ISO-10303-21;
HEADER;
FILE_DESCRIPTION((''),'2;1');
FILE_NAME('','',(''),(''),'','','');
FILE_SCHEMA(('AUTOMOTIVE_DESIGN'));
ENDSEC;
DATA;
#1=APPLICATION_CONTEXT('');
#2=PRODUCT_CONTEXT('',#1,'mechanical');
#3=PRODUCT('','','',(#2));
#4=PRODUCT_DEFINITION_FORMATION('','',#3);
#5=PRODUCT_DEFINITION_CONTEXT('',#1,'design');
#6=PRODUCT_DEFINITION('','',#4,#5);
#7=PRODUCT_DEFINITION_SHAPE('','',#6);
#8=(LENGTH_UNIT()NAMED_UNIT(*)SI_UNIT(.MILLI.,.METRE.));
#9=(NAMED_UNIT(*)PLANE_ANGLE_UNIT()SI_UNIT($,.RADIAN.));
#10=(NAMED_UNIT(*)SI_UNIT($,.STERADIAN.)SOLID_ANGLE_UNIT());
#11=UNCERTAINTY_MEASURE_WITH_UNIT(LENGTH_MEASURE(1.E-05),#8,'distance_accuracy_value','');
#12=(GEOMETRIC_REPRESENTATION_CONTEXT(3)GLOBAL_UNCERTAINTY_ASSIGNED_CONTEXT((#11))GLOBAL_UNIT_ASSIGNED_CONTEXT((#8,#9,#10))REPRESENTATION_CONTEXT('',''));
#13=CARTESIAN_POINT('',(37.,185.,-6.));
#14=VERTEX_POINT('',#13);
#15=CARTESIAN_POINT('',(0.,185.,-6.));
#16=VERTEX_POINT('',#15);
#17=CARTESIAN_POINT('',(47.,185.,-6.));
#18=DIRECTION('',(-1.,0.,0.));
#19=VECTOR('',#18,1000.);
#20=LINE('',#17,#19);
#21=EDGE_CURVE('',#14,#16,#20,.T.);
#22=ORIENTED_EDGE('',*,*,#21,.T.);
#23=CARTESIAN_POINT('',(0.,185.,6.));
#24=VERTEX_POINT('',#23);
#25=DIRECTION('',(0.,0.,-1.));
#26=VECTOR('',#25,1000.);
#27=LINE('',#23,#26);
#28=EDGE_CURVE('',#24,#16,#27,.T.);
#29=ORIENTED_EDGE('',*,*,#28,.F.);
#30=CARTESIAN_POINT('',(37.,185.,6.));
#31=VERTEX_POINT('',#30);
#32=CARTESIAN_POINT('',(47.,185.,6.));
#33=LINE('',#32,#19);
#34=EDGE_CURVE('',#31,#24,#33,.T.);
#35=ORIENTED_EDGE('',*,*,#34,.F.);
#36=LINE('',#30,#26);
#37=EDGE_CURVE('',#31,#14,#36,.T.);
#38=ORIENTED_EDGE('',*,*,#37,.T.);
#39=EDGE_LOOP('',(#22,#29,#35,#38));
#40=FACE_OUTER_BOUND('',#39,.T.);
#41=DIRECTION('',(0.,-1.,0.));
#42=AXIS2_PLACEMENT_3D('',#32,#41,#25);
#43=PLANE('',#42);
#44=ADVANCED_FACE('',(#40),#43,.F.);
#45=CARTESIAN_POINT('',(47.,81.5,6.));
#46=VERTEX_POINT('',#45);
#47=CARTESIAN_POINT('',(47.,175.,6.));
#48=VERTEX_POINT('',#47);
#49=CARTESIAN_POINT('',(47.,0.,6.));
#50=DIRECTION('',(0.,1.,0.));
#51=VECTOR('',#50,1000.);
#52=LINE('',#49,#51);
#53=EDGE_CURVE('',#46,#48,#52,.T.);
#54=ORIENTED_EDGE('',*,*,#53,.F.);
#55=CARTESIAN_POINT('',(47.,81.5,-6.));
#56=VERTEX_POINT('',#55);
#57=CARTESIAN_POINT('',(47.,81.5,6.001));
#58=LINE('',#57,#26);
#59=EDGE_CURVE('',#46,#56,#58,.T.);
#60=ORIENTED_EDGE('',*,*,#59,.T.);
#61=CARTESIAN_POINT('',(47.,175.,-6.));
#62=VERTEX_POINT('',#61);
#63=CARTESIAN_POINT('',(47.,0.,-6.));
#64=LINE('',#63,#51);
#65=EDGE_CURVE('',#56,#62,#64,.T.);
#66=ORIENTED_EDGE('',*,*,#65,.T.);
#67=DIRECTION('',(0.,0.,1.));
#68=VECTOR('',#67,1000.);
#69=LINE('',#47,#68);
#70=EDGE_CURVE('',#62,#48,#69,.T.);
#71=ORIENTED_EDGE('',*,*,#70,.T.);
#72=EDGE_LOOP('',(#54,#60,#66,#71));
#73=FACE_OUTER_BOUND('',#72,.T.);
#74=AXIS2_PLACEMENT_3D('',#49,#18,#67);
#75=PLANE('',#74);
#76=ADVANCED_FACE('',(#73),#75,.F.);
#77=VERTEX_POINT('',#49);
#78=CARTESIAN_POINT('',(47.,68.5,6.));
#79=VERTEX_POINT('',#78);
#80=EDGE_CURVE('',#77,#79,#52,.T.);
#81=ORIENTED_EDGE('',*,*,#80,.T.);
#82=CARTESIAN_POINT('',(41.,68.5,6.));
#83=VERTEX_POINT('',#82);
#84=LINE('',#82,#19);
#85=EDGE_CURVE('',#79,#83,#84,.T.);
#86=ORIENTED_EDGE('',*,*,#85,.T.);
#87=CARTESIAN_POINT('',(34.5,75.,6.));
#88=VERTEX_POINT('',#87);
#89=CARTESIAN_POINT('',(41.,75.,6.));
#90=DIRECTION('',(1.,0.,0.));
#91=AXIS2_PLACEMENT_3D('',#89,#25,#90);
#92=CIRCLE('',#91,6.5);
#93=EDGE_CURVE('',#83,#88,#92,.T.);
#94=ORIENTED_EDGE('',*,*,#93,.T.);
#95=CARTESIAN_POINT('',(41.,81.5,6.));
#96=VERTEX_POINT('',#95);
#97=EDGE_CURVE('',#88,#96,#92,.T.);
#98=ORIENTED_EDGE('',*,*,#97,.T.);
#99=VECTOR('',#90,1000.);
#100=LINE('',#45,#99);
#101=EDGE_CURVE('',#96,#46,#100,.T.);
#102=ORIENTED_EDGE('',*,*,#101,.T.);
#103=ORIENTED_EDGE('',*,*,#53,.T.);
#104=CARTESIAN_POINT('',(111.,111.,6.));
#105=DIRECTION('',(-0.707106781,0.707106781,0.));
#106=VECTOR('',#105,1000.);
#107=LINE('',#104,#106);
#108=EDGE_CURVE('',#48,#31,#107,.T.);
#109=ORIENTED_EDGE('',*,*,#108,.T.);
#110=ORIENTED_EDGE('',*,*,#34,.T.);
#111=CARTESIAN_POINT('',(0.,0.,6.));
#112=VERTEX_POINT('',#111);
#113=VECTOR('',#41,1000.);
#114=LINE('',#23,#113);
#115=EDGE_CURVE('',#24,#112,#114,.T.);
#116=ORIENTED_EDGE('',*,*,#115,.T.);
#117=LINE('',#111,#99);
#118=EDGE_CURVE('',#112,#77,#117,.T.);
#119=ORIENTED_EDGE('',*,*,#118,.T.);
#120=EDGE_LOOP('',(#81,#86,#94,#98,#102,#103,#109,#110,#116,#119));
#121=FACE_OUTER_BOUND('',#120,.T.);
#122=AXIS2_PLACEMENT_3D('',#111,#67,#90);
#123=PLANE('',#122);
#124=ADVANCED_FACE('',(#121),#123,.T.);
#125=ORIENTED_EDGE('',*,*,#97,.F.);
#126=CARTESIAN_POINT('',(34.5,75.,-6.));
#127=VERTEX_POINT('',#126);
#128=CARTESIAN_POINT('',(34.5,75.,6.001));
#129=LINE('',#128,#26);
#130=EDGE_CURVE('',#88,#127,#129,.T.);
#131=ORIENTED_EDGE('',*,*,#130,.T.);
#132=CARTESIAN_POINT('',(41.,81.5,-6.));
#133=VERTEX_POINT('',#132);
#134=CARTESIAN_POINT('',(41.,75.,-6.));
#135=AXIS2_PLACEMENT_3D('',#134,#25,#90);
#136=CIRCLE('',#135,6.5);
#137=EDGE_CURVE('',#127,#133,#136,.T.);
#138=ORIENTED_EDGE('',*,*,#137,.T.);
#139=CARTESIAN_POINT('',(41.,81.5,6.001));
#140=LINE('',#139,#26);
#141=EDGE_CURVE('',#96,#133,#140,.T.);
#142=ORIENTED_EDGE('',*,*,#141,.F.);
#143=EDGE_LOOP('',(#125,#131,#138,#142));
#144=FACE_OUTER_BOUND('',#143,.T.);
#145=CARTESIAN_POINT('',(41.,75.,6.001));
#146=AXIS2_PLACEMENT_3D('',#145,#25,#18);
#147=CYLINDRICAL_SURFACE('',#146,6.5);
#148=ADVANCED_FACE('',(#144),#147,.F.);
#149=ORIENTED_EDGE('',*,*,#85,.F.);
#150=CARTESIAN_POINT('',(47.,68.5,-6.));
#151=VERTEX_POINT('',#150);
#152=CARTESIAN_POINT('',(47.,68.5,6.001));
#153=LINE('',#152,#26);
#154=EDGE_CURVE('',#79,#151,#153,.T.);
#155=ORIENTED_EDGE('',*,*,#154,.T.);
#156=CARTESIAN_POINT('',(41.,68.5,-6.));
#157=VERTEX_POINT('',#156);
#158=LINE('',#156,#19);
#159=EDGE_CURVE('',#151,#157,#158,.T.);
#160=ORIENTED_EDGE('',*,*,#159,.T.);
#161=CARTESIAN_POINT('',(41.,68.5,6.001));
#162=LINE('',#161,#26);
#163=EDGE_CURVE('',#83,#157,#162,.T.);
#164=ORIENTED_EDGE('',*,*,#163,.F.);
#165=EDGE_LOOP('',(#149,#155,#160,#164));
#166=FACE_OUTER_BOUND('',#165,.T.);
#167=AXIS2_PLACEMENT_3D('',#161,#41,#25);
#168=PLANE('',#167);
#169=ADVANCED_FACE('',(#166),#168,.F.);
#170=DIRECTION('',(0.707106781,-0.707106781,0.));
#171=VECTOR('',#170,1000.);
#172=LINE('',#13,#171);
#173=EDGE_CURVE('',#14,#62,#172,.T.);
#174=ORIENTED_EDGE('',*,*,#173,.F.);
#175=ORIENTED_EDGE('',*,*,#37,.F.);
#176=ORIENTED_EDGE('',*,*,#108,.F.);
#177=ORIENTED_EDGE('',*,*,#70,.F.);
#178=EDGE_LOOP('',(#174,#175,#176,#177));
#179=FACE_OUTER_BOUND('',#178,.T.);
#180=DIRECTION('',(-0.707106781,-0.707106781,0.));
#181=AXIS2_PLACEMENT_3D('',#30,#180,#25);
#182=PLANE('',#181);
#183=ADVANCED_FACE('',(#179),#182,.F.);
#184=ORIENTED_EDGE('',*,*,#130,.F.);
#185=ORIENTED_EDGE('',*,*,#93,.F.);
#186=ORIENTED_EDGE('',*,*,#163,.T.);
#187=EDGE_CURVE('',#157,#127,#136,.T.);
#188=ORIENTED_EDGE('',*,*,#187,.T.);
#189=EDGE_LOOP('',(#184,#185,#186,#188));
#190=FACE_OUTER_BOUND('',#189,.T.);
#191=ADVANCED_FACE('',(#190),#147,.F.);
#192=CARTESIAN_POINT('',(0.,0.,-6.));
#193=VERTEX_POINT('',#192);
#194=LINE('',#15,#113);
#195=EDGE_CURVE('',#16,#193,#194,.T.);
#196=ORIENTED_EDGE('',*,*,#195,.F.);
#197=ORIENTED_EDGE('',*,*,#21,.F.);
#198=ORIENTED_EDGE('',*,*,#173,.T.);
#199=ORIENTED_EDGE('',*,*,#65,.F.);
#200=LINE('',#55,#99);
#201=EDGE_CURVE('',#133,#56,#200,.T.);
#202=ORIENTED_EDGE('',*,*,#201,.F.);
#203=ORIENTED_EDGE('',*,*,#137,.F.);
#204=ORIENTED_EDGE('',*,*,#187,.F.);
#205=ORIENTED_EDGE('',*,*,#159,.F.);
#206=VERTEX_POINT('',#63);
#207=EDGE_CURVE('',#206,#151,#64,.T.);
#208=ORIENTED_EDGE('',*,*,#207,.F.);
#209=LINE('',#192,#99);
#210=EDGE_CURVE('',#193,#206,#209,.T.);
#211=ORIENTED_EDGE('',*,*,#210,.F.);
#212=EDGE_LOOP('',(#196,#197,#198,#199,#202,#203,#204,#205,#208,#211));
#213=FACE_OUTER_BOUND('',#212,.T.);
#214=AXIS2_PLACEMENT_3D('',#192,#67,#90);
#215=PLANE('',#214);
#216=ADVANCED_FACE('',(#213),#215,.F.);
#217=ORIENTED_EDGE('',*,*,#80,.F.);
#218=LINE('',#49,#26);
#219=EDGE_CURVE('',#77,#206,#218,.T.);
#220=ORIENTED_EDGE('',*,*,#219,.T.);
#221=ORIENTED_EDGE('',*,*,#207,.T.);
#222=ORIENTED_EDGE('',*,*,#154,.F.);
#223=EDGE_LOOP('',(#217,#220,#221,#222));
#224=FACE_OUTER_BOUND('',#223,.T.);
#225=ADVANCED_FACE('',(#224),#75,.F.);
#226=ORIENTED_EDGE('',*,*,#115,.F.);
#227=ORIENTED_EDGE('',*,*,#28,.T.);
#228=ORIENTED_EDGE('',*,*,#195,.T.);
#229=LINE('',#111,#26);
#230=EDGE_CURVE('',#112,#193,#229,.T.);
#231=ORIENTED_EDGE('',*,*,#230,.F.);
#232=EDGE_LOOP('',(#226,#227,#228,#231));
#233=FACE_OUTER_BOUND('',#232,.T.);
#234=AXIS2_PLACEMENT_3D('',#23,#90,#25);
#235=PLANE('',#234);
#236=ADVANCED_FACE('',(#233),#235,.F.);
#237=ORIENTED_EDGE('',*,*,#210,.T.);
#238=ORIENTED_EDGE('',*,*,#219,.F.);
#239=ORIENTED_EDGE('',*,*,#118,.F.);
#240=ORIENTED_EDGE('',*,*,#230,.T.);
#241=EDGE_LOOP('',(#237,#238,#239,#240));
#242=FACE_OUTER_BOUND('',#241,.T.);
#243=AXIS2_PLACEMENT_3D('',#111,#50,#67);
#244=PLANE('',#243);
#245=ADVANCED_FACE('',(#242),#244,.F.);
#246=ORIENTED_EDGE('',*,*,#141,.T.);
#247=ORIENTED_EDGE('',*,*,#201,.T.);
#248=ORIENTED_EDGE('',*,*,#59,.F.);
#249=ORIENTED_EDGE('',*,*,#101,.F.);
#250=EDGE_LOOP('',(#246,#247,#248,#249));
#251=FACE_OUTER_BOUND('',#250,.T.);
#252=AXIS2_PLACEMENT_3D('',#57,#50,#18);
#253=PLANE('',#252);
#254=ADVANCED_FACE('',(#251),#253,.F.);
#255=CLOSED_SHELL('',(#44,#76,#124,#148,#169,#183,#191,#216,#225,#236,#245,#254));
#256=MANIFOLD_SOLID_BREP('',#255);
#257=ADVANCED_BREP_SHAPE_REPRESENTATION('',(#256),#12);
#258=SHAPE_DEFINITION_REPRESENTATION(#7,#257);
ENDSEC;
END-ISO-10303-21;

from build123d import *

# Parameters (mm, degrees)
SKETCH_1_W          = 47
SKETCH_1_H          = 185
EXTRUDE_1_DEPTH     = 6
CHAMFER_1_SIZE      = 10
CUT_EXTRUDE_2_REACH = 193.254


with BuildPart() as part:
    # 草图1 → 凸台-拉伸1 (new, symmetric)
    with BuildSketch(Plane.XY):
        with Locations((23.5, 92.5)):
            Rectangle(SKETCH_1_W, SKETCH_1_H)
    extrude(amount=EXTRUDE_1_DEPTH, both=True)

    # 倒角1
    chamfer_1_edges = [part.edges().sort_by_distance(p)[0] for p in [
        (47, 185, 0),
    ]]
    chamfer(chamfer_1_edges, length=CHAMFER_1_SIZE)

    # 草图3 → 切除-拉伸2 (cut, up to next)
    with BuildSketch(Plane(origin=(0, 0, -6), x_dir=(-1, 0, 0), z_dir=(0, 0, -1)), mode=Mode.PRIVATE) as cut_extrude_2_sk1:
        with BuildLine():
            Line((-47, 81.5), (-41, 81.5))
            ThreePointArc((-41, 81.5), (-34.5, 75), (-41, 68.5))
            Line((-41, 68.5), (-47, 68.5))
            Line((-47, 68.5), (-47, 81.5))
        make_face()
    cut_extrude_2_tool1 = extrude(cut_extrude_2_sk1.sketch, amount=-CUT_EXTRUDE_2_REACH, mode=Mode.PRIVATE) & part.part
    add(cut_extrude_2_tool1.solids().sort_by_distance((41.352691, 75, -6))[0], mode=Mode.SUBTRACT)


solid = part.part
